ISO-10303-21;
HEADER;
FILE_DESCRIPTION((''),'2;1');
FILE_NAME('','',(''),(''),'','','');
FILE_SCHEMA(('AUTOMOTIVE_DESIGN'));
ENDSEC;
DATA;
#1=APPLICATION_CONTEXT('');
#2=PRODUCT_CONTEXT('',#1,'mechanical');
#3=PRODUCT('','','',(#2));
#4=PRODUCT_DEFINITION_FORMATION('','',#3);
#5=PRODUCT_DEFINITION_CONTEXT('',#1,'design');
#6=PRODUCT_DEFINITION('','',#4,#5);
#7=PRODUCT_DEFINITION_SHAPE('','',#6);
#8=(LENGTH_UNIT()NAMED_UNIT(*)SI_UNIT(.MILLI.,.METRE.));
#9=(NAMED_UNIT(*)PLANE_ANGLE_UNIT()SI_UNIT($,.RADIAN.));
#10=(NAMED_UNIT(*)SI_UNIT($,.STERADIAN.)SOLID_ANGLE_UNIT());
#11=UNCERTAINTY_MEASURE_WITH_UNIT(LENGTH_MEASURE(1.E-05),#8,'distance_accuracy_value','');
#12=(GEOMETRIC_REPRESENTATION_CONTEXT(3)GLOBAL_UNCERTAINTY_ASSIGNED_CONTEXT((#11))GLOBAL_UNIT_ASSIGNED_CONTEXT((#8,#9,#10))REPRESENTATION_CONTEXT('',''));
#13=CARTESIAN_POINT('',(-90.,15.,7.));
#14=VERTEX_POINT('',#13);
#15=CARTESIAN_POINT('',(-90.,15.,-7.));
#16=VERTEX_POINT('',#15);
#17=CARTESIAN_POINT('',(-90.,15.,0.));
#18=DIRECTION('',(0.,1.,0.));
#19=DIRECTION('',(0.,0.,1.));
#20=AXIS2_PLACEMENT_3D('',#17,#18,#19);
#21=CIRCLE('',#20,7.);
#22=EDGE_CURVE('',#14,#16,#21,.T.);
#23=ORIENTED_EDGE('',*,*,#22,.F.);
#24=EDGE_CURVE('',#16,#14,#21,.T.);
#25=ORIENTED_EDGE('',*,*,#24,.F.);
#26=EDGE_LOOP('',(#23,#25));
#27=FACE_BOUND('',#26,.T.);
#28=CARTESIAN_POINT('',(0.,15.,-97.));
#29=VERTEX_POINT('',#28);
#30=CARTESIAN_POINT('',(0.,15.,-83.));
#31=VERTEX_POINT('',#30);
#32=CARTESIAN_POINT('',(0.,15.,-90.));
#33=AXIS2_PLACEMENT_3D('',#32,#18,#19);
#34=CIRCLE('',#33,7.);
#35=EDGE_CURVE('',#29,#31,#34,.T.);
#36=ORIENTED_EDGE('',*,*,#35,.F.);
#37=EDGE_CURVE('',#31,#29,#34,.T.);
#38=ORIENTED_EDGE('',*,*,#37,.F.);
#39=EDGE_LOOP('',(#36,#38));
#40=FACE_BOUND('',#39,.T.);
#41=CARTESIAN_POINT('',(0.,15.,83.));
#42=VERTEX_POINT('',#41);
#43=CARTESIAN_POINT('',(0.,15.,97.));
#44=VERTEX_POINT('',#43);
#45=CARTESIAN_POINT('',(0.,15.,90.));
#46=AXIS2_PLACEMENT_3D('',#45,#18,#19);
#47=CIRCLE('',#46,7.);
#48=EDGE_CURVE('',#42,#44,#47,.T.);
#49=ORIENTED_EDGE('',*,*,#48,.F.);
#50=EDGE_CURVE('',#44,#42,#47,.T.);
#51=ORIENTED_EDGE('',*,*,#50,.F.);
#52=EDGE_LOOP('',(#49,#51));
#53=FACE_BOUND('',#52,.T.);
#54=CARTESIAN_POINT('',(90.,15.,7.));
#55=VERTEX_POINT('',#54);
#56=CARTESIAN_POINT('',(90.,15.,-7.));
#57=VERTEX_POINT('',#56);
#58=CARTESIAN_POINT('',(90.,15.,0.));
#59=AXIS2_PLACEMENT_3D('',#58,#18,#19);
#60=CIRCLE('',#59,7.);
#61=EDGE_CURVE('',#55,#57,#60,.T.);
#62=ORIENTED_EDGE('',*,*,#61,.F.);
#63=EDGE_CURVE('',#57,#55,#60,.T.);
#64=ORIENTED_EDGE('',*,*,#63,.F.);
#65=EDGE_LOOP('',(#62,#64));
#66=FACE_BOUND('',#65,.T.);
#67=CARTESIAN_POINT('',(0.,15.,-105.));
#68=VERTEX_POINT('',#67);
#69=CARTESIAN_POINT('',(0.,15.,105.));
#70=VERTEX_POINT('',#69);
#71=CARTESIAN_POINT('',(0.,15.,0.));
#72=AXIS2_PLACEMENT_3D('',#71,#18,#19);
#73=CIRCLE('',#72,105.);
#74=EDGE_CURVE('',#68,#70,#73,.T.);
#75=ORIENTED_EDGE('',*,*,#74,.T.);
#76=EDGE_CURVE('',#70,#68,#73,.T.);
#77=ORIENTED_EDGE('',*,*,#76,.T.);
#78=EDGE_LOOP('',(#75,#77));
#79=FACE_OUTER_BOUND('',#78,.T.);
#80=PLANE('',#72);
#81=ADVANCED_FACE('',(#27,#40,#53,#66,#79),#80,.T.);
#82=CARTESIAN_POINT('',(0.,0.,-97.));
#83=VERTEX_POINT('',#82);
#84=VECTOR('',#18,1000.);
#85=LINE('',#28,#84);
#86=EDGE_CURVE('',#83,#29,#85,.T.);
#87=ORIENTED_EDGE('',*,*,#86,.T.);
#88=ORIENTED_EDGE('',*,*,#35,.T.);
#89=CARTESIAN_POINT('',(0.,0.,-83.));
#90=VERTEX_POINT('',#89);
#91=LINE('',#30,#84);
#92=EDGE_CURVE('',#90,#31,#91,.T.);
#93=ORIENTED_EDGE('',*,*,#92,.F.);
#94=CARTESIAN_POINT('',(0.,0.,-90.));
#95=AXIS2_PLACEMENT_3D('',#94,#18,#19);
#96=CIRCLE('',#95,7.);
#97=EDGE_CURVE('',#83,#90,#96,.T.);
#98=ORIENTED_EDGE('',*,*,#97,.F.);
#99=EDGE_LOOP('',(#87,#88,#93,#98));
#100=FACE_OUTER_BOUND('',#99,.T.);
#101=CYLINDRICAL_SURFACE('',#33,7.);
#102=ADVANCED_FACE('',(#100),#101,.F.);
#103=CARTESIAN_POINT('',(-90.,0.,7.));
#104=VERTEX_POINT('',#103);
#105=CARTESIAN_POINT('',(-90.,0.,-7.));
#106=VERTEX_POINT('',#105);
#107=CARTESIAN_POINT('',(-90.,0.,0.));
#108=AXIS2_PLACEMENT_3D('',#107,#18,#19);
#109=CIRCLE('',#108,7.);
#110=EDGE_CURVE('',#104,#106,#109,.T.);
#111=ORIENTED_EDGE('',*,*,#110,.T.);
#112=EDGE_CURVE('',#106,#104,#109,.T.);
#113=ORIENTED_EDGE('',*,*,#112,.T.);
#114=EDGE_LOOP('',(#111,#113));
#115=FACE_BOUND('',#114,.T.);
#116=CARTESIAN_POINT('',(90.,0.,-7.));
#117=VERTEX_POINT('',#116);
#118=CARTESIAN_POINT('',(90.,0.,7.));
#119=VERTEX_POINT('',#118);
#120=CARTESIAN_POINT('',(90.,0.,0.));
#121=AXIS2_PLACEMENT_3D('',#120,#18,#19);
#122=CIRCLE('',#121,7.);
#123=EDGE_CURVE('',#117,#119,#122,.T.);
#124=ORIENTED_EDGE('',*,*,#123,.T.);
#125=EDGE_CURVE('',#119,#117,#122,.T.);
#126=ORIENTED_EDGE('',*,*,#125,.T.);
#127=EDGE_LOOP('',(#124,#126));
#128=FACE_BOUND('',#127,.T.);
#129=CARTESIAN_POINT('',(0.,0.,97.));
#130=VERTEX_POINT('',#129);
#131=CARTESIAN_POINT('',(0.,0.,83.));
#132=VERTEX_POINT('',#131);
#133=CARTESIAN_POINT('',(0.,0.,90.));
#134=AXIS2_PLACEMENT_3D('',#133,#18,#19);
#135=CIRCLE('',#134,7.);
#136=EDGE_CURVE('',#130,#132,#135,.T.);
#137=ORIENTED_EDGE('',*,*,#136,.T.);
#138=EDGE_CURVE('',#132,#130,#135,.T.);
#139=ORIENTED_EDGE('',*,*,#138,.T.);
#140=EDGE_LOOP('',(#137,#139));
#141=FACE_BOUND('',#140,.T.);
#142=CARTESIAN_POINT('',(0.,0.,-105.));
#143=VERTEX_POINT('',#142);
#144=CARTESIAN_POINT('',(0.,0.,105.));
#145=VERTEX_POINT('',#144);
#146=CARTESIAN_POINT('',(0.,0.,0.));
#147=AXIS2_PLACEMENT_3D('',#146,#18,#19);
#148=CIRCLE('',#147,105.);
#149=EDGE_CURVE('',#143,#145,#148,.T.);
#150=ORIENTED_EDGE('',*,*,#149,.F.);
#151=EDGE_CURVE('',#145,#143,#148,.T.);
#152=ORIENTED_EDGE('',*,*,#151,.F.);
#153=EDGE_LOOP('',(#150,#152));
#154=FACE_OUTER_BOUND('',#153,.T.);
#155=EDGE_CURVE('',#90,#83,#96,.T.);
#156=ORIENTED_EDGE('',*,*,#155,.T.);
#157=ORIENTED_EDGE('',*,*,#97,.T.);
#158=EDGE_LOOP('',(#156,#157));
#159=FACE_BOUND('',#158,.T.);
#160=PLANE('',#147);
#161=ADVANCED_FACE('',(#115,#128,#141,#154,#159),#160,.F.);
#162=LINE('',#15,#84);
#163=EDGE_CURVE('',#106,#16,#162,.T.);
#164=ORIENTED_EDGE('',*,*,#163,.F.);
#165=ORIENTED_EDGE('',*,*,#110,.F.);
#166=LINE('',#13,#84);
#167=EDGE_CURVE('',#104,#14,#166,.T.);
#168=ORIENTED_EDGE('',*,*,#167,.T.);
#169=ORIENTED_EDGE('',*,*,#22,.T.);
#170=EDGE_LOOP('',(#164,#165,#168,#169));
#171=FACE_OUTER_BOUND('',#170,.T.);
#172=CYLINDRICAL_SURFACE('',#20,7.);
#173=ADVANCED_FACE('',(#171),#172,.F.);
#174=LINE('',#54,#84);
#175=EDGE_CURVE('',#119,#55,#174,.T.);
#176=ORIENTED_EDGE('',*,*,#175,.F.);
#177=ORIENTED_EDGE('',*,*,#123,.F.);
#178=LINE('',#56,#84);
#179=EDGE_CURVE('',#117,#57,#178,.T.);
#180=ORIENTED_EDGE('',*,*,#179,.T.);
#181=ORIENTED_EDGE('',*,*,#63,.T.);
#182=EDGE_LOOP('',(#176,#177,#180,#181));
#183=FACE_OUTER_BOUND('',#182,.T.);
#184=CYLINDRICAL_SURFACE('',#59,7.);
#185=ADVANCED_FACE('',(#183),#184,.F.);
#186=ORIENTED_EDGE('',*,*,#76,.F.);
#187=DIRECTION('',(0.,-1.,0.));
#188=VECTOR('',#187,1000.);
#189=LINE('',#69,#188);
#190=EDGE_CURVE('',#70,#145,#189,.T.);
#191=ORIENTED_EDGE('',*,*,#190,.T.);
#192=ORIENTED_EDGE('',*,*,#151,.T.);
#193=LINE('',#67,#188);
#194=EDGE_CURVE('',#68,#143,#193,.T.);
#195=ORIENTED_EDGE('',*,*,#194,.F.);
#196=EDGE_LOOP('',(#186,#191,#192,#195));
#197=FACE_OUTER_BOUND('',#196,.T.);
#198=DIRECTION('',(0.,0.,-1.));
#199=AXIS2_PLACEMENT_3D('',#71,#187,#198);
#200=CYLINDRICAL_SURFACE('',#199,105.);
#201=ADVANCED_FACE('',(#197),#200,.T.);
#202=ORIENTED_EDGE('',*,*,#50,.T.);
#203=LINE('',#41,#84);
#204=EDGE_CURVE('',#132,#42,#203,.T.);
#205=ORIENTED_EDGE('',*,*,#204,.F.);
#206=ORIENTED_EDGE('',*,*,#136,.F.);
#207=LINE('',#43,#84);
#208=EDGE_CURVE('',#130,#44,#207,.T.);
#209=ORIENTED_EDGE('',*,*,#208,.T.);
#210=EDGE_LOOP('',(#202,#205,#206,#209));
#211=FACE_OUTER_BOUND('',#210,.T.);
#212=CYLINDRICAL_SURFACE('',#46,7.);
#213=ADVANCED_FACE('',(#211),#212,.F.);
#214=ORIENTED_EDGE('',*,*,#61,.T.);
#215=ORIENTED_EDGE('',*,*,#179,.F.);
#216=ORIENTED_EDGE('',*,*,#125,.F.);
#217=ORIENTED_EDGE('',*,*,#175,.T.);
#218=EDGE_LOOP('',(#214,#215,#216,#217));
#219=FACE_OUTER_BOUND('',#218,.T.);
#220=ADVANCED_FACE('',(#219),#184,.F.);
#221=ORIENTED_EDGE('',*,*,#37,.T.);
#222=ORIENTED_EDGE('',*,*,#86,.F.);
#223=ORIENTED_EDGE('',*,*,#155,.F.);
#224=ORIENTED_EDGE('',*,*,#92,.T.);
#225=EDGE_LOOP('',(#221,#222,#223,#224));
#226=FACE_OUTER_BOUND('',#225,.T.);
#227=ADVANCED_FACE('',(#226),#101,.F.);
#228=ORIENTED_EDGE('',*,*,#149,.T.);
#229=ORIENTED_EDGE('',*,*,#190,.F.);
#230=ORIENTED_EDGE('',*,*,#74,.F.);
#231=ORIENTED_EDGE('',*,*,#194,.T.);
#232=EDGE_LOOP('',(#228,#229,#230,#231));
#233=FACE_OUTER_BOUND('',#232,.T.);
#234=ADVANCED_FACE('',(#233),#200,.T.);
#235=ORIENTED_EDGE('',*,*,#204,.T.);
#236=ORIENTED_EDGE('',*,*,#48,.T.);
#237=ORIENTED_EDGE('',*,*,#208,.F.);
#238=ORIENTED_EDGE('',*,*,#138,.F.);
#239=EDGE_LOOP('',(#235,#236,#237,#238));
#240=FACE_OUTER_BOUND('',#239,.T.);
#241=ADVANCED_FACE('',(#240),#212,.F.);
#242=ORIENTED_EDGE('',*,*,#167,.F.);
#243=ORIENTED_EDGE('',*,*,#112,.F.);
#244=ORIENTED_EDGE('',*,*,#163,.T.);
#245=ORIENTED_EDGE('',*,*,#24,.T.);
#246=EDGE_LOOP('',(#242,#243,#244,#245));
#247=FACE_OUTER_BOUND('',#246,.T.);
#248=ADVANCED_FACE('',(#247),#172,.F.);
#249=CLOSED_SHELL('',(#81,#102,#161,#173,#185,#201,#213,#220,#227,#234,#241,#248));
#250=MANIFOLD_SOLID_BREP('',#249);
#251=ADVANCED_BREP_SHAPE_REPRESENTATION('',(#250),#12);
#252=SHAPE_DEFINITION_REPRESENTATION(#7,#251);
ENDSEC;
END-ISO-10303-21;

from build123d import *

# Parameters (mm, degrees)
SKETCH1_R                  = 105
BOSS_EXTRUDE1_DEPTH        = 15
F_14_0_14_DIAMETER_HOLE1_D = 14


with BuildPart() as part:
    # Sketch1 → Boss-Extrude1 (new body)
    with BuildSketch(Plane(origin=(0, 0, 0), x_dir=(1, 0, 0), z_dir=(0, 1, 0))):
        with Locations(Location((0, 0, 0), (0, 0, 270))):
            Circle(SKETCH1_R)
    extrude(amount=BOSS_EXTRUDE1_DEPTH)

    # Ø14.0 (14) Diameter Hole1 (through all)
    with Locations(Plane(origin=(0, 15, 0), x_dir=(1, 0, 0), z_dir=(0, 1, 0))):
        with Locations((0, 90), (90, 0), (0, -90), (-90, 0)):
            Hole(F_14_0_14_DIAMETER_HOLE1_D / 2)


solid = part.part
